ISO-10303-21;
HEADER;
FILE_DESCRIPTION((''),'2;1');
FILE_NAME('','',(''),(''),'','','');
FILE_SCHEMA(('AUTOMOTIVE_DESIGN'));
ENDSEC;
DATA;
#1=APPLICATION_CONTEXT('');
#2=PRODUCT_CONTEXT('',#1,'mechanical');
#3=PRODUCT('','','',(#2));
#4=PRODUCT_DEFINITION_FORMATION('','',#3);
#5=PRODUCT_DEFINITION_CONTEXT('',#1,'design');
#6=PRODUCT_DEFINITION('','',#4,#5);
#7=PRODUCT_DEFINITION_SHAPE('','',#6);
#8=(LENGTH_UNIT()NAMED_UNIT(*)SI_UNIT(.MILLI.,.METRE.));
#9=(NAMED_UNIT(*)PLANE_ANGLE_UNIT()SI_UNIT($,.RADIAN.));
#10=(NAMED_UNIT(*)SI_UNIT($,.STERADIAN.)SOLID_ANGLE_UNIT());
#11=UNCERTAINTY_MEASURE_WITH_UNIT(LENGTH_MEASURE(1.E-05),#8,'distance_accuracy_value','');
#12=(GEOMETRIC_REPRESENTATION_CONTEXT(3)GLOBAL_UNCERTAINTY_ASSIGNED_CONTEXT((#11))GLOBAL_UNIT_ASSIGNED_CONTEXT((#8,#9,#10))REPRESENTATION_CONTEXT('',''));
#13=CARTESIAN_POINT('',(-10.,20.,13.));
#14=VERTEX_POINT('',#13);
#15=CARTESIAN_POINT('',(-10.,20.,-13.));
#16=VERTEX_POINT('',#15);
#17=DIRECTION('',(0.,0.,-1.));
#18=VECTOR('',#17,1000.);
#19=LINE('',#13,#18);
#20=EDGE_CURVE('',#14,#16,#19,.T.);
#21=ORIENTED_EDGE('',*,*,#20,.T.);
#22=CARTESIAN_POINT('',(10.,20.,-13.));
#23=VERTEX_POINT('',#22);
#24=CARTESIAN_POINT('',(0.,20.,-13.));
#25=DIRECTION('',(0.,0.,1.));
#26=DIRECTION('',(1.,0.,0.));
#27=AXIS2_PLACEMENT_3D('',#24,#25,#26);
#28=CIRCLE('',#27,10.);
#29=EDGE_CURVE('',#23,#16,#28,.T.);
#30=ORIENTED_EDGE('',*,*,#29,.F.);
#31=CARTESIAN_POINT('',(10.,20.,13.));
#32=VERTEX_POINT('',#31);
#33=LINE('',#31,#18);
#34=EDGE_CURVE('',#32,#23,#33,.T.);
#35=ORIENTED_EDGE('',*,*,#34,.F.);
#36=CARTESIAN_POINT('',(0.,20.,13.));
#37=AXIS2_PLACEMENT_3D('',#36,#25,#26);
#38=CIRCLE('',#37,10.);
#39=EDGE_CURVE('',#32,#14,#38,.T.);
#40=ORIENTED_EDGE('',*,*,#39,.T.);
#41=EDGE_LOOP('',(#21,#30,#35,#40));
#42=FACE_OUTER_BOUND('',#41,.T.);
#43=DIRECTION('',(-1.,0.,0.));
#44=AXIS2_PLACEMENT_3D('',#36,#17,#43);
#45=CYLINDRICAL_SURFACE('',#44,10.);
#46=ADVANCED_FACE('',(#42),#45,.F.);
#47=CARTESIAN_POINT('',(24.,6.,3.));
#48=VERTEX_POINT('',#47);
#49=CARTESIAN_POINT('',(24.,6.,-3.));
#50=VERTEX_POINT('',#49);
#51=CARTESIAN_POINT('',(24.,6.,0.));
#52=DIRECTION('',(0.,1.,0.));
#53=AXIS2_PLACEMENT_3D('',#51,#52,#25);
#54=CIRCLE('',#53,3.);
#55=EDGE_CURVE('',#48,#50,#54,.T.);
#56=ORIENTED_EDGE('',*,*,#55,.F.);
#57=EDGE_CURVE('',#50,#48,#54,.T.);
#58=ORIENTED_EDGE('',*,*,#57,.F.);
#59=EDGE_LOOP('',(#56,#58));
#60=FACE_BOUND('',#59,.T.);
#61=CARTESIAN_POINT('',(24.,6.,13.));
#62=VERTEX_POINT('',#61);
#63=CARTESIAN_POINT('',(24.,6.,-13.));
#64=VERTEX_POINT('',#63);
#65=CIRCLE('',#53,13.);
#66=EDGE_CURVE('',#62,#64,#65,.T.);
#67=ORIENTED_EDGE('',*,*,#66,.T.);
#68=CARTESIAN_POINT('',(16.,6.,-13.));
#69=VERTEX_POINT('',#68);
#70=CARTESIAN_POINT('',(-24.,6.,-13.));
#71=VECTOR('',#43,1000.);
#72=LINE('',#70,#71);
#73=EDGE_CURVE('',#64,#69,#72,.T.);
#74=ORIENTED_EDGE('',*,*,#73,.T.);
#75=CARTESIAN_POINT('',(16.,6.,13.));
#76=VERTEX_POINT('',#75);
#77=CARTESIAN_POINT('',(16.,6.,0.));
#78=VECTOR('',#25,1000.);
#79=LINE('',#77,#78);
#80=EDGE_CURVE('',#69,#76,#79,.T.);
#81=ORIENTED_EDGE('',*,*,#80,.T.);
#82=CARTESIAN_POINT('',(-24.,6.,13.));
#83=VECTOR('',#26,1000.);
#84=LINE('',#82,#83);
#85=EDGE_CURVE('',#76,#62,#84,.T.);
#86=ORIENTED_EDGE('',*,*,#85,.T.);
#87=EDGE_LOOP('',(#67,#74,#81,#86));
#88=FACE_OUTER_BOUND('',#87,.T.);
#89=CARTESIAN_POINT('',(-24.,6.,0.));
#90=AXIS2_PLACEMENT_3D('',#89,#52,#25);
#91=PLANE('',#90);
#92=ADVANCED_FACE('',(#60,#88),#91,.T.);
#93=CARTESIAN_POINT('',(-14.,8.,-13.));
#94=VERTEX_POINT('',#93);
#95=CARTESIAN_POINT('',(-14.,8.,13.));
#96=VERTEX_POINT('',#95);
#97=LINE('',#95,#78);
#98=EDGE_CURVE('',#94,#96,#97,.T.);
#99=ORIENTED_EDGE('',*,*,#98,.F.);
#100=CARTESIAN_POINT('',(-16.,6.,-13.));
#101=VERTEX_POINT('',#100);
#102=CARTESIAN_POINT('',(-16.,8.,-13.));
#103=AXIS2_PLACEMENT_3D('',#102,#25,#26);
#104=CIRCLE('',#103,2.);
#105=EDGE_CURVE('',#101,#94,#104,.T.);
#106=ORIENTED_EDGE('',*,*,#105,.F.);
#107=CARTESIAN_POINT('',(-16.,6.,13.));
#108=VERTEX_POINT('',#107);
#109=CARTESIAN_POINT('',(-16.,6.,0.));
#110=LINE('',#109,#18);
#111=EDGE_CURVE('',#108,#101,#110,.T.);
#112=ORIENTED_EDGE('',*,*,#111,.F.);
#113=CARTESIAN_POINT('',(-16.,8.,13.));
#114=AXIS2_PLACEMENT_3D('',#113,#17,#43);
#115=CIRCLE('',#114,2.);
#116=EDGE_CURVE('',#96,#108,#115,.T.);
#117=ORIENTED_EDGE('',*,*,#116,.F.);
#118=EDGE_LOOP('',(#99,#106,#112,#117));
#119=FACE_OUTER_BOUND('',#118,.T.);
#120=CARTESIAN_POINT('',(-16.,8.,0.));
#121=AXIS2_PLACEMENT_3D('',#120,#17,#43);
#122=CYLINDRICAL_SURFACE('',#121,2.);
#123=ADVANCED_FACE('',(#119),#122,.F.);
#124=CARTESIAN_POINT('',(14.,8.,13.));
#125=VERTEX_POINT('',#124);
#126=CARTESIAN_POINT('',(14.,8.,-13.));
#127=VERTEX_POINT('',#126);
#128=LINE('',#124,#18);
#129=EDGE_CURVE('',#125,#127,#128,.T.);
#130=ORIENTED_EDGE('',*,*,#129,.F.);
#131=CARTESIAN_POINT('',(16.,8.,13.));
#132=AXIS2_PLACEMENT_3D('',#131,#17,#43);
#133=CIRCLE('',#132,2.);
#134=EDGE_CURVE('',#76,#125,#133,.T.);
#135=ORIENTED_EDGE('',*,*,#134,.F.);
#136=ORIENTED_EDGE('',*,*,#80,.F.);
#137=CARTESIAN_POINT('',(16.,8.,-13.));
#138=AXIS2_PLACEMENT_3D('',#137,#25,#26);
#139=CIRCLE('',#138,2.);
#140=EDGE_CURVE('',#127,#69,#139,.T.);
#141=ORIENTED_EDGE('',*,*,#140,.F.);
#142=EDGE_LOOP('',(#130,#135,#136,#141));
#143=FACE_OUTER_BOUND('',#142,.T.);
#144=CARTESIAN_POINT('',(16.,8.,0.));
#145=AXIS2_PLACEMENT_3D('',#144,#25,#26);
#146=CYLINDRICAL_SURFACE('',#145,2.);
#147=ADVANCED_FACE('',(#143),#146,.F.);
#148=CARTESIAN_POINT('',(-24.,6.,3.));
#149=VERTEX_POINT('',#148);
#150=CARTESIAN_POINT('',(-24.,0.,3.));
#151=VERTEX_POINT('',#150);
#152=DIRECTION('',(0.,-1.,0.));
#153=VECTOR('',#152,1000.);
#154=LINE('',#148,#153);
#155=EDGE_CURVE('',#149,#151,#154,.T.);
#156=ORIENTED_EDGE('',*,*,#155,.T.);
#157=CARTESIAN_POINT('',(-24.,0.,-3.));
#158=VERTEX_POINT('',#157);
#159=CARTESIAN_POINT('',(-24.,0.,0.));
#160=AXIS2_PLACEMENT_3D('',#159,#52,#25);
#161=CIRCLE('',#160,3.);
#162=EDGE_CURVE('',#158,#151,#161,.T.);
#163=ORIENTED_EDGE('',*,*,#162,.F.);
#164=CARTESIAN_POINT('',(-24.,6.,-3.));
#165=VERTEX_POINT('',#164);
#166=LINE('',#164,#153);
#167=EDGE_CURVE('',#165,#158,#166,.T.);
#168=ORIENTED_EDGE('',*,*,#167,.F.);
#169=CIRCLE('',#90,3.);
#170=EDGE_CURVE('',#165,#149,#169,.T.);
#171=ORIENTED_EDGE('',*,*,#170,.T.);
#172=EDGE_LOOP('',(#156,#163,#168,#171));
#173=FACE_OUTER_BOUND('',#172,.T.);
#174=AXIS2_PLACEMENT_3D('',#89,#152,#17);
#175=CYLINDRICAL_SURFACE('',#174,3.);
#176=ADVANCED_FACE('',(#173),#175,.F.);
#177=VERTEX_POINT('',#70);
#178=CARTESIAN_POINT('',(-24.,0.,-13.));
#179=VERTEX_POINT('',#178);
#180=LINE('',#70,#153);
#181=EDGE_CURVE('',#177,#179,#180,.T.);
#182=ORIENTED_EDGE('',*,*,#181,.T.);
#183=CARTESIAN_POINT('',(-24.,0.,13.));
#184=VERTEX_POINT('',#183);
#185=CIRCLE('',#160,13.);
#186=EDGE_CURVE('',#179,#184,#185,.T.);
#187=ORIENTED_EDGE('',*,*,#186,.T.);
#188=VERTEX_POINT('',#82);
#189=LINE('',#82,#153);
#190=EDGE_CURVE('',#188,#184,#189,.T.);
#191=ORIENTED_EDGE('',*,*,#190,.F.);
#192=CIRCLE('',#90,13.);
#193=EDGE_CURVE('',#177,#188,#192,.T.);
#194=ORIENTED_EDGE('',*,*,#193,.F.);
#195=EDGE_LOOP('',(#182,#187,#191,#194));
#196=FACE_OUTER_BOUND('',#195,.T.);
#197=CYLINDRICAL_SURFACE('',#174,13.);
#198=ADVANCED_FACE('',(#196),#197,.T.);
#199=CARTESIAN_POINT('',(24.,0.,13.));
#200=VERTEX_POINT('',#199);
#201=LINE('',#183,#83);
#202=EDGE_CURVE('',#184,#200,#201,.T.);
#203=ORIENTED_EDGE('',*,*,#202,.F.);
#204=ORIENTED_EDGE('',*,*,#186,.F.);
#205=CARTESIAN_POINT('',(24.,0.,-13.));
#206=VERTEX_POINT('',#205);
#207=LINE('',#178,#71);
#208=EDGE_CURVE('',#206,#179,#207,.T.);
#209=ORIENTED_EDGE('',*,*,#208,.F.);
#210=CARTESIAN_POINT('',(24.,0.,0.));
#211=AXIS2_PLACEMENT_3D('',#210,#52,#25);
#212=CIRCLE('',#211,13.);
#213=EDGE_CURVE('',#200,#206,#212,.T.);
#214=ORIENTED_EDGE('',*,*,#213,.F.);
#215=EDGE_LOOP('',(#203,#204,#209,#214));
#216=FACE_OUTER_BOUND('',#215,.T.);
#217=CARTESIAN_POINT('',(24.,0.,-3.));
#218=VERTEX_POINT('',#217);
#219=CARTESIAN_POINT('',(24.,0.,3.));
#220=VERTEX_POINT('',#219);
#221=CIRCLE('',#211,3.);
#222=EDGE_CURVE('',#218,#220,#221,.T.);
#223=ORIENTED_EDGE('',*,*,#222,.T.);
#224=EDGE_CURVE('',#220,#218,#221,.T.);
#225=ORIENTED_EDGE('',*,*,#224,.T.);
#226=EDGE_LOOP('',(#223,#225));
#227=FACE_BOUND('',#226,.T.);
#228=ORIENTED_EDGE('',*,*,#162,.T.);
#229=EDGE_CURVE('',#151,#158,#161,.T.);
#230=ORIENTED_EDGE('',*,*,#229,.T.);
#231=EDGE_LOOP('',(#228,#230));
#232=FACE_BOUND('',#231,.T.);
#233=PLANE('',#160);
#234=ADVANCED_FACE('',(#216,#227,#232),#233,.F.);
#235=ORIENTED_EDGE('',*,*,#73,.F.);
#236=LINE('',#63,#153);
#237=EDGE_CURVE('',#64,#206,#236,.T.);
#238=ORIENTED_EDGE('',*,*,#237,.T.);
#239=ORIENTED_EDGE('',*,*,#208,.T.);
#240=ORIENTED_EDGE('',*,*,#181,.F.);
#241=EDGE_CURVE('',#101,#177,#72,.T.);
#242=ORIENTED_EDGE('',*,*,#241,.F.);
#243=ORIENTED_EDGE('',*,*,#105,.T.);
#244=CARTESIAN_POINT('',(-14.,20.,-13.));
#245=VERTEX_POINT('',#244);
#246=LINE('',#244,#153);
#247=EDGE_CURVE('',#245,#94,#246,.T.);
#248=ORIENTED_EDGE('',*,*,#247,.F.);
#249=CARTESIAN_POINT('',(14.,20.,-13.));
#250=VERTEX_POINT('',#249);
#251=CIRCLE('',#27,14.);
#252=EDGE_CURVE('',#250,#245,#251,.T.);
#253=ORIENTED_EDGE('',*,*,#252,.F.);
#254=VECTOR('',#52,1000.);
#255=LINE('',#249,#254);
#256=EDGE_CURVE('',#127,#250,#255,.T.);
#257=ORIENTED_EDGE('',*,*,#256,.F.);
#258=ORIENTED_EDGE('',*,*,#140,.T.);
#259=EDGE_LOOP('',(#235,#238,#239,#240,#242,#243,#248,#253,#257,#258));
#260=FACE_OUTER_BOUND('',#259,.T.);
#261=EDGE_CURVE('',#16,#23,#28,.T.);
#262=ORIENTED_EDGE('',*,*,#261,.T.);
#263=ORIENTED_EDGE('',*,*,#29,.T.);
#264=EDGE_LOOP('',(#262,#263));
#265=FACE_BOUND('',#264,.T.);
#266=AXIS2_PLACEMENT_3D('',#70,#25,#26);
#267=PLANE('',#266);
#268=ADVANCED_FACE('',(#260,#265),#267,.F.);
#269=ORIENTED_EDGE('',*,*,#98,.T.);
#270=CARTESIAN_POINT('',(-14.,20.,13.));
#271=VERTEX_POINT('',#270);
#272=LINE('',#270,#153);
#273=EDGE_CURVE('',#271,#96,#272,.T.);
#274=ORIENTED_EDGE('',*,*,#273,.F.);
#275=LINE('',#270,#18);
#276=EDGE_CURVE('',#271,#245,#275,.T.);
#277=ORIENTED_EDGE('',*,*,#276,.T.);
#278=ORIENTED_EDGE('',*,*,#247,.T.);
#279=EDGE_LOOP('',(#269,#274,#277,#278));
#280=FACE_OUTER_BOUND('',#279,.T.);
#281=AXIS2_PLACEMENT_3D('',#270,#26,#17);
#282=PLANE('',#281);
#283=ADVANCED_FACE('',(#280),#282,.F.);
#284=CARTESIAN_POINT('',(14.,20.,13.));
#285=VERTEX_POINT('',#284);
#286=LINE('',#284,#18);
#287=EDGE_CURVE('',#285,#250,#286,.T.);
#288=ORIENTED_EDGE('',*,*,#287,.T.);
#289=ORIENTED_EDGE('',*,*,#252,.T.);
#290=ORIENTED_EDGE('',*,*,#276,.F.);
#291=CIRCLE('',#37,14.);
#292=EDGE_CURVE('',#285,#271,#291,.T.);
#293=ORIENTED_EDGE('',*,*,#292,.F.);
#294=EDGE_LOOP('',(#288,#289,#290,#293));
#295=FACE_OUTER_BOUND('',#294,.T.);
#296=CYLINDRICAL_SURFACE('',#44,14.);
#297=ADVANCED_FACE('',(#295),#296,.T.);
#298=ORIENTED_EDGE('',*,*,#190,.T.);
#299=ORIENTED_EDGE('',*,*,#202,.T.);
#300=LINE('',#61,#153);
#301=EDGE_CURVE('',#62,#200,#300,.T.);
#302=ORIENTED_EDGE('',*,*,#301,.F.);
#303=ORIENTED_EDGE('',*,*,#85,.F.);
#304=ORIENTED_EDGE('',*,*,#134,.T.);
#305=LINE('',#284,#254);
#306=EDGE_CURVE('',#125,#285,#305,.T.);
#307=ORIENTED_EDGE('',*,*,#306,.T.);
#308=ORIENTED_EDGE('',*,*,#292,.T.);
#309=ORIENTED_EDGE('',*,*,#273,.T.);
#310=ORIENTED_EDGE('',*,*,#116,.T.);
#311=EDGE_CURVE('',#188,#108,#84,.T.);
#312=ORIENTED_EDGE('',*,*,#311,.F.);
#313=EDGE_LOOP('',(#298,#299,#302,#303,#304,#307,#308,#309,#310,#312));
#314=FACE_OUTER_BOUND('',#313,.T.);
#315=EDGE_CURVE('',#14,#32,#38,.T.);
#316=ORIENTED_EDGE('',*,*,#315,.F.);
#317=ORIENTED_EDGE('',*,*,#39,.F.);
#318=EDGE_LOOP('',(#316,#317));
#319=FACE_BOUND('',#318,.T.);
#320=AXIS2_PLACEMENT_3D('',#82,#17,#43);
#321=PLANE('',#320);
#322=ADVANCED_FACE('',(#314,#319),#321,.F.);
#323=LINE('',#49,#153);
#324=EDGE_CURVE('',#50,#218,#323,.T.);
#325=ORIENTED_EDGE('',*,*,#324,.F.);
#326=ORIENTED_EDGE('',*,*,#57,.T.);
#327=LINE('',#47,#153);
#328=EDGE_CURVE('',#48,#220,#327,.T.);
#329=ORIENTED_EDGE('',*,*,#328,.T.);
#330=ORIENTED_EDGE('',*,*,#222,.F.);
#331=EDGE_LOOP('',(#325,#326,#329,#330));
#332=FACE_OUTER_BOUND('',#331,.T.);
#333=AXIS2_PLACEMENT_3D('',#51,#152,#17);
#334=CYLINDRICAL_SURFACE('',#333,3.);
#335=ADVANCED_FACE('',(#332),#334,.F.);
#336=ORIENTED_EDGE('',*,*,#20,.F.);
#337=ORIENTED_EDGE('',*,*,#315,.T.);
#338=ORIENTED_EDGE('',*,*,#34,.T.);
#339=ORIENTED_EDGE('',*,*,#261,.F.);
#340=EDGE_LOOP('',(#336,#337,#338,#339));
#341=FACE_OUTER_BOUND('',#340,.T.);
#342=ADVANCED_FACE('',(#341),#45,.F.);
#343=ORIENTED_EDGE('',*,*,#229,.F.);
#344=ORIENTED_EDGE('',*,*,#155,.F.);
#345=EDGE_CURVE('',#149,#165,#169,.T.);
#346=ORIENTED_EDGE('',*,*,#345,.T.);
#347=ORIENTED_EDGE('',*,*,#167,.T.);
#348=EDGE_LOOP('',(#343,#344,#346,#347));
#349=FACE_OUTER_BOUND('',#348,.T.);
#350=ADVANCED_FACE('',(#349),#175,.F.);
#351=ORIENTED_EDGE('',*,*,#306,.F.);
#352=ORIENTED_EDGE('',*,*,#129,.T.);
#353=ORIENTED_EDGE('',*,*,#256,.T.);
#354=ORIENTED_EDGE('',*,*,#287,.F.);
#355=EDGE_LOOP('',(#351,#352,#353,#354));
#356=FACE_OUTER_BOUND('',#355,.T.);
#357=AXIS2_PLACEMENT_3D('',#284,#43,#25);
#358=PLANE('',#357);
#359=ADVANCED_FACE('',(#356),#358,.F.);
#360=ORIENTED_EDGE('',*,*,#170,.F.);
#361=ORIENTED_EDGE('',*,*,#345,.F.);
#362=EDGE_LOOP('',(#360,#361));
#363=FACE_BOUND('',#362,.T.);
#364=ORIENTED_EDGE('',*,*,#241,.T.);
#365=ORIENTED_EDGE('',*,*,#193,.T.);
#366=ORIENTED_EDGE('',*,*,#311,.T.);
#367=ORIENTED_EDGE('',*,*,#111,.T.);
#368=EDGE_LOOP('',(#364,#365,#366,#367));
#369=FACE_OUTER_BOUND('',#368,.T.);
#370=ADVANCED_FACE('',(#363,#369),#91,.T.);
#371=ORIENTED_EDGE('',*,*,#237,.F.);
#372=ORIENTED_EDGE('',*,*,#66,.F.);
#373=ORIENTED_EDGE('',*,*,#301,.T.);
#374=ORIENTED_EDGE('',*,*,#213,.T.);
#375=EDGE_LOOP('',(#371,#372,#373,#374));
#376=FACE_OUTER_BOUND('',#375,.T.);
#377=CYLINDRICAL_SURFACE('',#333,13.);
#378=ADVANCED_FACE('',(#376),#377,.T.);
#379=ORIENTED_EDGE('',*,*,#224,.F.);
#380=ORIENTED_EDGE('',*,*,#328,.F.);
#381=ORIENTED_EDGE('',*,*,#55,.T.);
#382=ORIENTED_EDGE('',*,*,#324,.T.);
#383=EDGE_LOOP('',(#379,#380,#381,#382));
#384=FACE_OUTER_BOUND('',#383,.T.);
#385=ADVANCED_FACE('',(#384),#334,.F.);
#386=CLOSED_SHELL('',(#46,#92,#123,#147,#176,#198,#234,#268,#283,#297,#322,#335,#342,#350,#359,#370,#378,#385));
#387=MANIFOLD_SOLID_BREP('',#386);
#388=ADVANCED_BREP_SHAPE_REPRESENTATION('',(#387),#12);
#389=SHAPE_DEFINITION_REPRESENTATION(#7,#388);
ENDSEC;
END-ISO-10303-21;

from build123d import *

# Parameters (mm, degrees)
SKETCH1_R           = 3
BOSS_EXTRUDE1_DEPTH = 6
SKETCH2_R           = 10
BOSS_EXTRUDE2_DEPTH = 13
FILLET1_R           = 2


with BuildPart() as part:
    # Sketch1 → Boss-Extrude1 (new body)
    with BuildSketch(Plane(origin=(0, 0, 0), x_dir=(1, 0, 0), z_dir=(0, 1, 0))):
        with BuildLine():
            Line((-24, 13), (24, 13))
            ThreePointArc((24, 13), (37, 0), (24, -13))
            Line((24, -13), (-24, -13))
            ThreePointArc((-24, -13), (-37, 0), (-24, 13))
        make_face()
        with Locations(Location((-24, 0, 0), (0, 0, 270))):
            Circle(SKETCH1_R, mode=Mode.SUBTRACT)
        with Locations(Location((24, 0, 0), (0, 0, 270))):
            Circle(SKETCH1_R, mode=Mode.SUBTRACT)
    extrude(amount=BOSS_EXTRUDE1_DEPTH)

    # Sketch2 → Boss-Extrude2 (add, symmetric)
    with BuildSketch(Plane.XY):
        with BuildLine():
            Line((-14, 20), (-14, 0))
            Line((-14, 0), (14, 0))
            Line((14, 0), (14, 20))
            ThreePointArc((14, 20), (0, 34), (-14, 20))
        make_face()
        with Locations(Location((0, 20, 0), (0, 0, 180))):
            Circle(SKETCH2_R, mode=Mode.SUBTRACT)
    extrude(amount=BOSS_EXTRUDE2_DEPTH, both=True)

    # Fillet1
    fillet1_edges = [part.edges().sort_by_distance(p)[0] for p in [
        (-14, 6, 0),
        (14, 6, 0),
    ]]
    fillet(fillet1_edges, radius=FILLET1_R)


solid = part.part
